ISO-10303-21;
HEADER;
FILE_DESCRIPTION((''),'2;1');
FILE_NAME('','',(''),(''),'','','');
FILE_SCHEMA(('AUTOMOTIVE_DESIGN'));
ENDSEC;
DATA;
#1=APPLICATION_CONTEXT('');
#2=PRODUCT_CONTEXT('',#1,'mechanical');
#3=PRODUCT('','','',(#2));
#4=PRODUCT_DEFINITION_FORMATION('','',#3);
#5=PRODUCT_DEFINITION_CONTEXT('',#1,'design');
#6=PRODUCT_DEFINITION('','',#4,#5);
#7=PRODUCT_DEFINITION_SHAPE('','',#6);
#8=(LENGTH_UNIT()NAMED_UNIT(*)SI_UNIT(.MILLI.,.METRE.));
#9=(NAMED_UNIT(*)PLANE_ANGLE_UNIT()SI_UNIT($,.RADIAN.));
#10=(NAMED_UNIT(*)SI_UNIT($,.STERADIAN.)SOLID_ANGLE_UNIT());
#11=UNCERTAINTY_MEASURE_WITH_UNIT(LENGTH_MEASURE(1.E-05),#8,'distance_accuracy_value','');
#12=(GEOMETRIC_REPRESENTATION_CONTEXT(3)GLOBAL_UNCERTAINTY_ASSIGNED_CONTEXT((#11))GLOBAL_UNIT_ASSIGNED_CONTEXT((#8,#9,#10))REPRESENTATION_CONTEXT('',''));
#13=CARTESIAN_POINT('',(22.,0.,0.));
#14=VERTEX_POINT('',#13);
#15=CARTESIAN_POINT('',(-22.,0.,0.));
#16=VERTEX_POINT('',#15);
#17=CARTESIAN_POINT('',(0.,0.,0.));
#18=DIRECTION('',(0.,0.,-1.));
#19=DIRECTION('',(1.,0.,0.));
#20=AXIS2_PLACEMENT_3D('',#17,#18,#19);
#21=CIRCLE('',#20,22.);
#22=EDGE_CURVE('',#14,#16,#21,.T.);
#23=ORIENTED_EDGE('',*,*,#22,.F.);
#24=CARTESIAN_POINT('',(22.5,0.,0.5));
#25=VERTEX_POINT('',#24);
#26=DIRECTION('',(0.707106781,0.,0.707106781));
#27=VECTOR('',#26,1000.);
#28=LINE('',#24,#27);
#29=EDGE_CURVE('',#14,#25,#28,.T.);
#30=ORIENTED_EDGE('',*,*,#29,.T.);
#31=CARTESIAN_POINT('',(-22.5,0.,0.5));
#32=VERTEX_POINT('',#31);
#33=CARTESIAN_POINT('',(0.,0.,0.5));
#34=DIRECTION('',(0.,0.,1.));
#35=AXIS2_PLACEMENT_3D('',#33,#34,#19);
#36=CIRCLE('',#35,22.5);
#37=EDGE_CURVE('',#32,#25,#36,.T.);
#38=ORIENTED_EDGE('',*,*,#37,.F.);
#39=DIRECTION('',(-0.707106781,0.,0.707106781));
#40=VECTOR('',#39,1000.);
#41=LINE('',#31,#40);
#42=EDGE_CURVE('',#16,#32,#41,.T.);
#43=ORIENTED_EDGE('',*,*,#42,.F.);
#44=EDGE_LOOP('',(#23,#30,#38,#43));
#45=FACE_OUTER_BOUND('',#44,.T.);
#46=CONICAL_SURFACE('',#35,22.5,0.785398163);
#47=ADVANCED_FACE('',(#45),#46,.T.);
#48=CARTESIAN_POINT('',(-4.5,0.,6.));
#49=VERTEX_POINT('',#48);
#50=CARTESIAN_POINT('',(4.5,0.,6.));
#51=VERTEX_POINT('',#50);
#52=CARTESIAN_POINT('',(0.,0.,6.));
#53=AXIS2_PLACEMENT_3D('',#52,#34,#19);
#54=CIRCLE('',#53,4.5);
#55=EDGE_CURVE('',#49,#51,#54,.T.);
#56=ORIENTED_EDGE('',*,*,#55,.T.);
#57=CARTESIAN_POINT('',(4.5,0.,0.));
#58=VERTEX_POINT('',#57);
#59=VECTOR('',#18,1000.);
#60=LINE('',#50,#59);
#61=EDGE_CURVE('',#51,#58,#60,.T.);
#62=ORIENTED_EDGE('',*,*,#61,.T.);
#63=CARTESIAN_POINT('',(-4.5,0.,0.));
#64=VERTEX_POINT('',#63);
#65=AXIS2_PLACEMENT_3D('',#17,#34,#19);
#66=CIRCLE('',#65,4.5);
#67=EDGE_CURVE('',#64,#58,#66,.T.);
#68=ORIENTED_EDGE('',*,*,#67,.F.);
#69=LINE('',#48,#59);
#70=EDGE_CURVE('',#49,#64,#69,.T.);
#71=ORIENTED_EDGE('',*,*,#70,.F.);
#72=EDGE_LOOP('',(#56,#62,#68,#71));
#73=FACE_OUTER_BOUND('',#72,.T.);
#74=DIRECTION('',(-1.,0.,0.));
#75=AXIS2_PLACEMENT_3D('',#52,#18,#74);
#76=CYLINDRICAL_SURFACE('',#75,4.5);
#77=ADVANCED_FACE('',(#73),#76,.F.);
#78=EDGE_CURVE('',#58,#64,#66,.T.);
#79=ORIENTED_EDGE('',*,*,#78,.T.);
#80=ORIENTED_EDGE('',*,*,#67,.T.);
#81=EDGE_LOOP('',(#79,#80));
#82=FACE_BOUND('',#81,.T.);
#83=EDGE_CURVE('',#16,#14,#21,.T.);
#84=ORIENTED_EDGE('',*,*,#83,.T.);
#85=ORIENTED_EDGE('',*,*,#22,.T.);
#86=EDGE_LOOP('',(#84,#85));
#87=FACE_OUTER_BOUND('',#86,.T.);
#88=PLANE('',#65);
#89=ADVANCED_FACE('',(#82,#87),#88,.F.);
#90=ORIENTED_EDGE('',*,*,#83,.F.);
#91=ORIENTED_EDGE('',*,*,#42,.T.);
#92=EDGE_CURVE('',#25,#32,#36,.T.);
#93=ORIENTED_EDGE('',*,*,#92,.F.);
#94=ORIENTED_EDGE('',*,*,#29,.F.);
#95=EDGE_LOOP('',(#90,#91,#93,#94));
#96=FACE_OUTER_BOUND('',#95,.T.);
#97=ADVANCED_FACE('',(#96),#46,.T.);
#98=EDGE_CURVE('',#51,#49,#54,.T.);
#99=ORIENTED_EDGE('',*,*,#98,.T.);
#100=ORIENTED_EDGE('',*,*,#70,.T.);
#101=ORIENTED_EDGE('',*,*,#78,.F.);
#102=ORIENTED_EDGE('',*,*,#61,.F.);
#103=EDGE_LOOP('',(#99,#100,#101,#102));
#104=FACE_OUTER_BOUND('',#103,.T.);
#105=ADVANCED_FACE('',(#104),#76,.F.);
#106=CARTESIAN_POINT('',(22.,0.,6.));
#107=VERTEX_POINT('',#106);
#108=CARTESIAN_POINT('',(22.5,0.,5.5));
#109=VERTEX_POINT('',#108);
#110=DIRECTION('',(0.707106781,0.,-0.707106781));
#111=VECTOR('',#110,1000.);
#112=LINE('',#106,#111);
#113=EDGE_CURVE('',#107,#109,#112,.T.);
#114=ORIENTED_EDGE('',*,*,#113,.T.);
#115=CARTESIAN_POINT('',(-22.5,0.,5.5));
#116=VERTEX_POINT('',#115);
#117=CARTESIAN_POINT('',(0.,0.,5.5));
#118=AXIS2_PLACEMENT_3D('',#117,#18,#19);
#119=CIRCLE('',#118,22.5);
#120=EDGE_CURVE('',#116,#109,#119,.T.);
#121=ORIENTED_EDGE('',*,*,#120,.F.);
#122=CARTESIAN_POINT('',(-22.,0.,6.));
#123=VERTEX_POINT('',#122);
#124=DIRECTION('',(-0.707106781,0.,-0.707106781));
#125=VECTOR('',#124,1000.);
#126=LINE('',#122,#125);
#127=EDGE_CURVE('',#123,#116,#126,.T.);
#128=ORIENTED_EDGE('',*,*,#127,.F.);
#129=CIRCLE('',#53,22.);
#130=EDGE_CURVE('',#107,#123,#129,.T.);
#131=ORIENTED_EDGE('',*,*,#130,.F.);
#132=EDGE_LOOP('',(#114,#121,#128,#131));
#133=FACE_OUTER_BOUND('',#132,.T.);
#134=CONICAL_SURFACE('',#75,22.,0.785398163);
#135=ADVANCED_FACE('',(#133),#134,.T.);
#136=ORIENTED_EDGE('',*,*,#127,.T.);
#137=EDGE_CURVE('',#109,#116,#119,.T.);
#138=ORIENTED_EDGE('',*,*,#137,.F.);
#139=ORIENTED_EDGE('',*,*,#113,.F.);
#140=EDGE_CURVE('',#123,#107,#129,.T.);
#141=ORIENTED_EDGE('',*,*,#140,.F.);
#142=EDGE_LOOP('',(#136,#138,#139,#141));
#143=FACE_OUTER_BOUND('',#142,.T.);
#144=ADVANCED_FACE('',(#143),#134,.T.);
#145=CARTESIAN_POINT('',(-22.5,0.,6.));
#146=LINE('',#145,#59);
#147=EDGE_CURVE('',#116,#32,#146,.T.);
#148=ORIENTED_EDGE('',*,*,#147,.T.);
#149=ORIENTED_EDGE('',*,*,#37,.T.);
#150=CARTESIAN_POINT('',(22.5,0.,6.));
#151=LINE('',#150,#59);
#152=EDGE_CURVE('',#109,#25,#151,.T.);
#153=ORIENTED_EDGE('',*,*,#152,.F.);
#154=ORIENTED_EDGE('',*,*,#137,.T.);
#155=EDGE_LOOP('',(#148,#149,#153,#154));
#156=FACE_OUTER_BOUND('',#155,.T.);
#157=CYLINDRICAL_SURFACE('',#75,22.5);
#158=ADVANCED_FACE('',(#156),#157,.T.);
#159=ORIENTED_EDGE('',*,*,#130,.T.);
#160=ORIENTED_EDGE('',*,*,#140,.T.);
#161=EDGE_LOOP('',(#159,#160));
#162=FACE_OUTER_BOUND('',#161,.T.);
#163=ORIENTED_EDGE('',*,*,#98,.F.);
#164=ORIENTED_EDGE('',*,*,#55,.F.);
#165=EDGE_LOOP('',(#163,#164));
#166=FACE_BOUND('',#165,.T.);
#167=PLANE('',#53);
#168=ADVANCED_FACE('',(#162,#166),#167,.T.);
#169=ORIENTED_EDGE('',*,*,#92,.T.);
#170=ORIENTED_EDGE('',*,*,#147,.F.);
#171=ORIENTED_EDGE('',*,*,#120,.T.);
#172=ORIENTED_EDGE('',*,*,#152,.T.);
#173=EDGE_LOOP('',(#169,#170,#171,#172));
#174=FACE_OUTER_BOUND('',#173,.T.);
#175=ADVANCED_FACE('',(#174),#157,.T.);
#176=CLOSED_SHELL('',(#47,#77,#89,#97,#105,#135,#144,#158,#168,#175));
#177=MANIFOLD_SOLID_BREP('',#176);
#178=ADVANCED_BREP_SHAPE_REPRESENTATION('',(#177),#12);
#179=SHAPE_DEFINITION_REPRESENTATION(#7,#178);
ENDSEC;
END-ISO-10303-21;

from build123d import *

# Parameters (mm, degrees)
SKETCH_1_R      = 22.5
SKETCH_1_R_2    = 4.5
EXTRUDE_1_DEPTH = 6
CHAMFER_1_SIZE  = 0.5


with BuildPart() as part:
    # 草图1 → 凸台-拉伸1 (new body)
    with BuildSketch(Plane.XY):
        Circle(SKETCH_1_R)
        Circle(SKETCH_1_R_2, mode=Mode.SUBTRACT)
    extrude(amount=EXTRUDE_1_DEPTH)

    # 倒角1
    chamfer_1_edges = [part.edges().sort_by_distance(p)[0] for p in [
        (-22.5, 0, 0),
        (-22.5, 0, 6),
    ]]
    chamfer(chamfer_1_edges, length=CHAMFER_1_SIZE)


solid = part.part
